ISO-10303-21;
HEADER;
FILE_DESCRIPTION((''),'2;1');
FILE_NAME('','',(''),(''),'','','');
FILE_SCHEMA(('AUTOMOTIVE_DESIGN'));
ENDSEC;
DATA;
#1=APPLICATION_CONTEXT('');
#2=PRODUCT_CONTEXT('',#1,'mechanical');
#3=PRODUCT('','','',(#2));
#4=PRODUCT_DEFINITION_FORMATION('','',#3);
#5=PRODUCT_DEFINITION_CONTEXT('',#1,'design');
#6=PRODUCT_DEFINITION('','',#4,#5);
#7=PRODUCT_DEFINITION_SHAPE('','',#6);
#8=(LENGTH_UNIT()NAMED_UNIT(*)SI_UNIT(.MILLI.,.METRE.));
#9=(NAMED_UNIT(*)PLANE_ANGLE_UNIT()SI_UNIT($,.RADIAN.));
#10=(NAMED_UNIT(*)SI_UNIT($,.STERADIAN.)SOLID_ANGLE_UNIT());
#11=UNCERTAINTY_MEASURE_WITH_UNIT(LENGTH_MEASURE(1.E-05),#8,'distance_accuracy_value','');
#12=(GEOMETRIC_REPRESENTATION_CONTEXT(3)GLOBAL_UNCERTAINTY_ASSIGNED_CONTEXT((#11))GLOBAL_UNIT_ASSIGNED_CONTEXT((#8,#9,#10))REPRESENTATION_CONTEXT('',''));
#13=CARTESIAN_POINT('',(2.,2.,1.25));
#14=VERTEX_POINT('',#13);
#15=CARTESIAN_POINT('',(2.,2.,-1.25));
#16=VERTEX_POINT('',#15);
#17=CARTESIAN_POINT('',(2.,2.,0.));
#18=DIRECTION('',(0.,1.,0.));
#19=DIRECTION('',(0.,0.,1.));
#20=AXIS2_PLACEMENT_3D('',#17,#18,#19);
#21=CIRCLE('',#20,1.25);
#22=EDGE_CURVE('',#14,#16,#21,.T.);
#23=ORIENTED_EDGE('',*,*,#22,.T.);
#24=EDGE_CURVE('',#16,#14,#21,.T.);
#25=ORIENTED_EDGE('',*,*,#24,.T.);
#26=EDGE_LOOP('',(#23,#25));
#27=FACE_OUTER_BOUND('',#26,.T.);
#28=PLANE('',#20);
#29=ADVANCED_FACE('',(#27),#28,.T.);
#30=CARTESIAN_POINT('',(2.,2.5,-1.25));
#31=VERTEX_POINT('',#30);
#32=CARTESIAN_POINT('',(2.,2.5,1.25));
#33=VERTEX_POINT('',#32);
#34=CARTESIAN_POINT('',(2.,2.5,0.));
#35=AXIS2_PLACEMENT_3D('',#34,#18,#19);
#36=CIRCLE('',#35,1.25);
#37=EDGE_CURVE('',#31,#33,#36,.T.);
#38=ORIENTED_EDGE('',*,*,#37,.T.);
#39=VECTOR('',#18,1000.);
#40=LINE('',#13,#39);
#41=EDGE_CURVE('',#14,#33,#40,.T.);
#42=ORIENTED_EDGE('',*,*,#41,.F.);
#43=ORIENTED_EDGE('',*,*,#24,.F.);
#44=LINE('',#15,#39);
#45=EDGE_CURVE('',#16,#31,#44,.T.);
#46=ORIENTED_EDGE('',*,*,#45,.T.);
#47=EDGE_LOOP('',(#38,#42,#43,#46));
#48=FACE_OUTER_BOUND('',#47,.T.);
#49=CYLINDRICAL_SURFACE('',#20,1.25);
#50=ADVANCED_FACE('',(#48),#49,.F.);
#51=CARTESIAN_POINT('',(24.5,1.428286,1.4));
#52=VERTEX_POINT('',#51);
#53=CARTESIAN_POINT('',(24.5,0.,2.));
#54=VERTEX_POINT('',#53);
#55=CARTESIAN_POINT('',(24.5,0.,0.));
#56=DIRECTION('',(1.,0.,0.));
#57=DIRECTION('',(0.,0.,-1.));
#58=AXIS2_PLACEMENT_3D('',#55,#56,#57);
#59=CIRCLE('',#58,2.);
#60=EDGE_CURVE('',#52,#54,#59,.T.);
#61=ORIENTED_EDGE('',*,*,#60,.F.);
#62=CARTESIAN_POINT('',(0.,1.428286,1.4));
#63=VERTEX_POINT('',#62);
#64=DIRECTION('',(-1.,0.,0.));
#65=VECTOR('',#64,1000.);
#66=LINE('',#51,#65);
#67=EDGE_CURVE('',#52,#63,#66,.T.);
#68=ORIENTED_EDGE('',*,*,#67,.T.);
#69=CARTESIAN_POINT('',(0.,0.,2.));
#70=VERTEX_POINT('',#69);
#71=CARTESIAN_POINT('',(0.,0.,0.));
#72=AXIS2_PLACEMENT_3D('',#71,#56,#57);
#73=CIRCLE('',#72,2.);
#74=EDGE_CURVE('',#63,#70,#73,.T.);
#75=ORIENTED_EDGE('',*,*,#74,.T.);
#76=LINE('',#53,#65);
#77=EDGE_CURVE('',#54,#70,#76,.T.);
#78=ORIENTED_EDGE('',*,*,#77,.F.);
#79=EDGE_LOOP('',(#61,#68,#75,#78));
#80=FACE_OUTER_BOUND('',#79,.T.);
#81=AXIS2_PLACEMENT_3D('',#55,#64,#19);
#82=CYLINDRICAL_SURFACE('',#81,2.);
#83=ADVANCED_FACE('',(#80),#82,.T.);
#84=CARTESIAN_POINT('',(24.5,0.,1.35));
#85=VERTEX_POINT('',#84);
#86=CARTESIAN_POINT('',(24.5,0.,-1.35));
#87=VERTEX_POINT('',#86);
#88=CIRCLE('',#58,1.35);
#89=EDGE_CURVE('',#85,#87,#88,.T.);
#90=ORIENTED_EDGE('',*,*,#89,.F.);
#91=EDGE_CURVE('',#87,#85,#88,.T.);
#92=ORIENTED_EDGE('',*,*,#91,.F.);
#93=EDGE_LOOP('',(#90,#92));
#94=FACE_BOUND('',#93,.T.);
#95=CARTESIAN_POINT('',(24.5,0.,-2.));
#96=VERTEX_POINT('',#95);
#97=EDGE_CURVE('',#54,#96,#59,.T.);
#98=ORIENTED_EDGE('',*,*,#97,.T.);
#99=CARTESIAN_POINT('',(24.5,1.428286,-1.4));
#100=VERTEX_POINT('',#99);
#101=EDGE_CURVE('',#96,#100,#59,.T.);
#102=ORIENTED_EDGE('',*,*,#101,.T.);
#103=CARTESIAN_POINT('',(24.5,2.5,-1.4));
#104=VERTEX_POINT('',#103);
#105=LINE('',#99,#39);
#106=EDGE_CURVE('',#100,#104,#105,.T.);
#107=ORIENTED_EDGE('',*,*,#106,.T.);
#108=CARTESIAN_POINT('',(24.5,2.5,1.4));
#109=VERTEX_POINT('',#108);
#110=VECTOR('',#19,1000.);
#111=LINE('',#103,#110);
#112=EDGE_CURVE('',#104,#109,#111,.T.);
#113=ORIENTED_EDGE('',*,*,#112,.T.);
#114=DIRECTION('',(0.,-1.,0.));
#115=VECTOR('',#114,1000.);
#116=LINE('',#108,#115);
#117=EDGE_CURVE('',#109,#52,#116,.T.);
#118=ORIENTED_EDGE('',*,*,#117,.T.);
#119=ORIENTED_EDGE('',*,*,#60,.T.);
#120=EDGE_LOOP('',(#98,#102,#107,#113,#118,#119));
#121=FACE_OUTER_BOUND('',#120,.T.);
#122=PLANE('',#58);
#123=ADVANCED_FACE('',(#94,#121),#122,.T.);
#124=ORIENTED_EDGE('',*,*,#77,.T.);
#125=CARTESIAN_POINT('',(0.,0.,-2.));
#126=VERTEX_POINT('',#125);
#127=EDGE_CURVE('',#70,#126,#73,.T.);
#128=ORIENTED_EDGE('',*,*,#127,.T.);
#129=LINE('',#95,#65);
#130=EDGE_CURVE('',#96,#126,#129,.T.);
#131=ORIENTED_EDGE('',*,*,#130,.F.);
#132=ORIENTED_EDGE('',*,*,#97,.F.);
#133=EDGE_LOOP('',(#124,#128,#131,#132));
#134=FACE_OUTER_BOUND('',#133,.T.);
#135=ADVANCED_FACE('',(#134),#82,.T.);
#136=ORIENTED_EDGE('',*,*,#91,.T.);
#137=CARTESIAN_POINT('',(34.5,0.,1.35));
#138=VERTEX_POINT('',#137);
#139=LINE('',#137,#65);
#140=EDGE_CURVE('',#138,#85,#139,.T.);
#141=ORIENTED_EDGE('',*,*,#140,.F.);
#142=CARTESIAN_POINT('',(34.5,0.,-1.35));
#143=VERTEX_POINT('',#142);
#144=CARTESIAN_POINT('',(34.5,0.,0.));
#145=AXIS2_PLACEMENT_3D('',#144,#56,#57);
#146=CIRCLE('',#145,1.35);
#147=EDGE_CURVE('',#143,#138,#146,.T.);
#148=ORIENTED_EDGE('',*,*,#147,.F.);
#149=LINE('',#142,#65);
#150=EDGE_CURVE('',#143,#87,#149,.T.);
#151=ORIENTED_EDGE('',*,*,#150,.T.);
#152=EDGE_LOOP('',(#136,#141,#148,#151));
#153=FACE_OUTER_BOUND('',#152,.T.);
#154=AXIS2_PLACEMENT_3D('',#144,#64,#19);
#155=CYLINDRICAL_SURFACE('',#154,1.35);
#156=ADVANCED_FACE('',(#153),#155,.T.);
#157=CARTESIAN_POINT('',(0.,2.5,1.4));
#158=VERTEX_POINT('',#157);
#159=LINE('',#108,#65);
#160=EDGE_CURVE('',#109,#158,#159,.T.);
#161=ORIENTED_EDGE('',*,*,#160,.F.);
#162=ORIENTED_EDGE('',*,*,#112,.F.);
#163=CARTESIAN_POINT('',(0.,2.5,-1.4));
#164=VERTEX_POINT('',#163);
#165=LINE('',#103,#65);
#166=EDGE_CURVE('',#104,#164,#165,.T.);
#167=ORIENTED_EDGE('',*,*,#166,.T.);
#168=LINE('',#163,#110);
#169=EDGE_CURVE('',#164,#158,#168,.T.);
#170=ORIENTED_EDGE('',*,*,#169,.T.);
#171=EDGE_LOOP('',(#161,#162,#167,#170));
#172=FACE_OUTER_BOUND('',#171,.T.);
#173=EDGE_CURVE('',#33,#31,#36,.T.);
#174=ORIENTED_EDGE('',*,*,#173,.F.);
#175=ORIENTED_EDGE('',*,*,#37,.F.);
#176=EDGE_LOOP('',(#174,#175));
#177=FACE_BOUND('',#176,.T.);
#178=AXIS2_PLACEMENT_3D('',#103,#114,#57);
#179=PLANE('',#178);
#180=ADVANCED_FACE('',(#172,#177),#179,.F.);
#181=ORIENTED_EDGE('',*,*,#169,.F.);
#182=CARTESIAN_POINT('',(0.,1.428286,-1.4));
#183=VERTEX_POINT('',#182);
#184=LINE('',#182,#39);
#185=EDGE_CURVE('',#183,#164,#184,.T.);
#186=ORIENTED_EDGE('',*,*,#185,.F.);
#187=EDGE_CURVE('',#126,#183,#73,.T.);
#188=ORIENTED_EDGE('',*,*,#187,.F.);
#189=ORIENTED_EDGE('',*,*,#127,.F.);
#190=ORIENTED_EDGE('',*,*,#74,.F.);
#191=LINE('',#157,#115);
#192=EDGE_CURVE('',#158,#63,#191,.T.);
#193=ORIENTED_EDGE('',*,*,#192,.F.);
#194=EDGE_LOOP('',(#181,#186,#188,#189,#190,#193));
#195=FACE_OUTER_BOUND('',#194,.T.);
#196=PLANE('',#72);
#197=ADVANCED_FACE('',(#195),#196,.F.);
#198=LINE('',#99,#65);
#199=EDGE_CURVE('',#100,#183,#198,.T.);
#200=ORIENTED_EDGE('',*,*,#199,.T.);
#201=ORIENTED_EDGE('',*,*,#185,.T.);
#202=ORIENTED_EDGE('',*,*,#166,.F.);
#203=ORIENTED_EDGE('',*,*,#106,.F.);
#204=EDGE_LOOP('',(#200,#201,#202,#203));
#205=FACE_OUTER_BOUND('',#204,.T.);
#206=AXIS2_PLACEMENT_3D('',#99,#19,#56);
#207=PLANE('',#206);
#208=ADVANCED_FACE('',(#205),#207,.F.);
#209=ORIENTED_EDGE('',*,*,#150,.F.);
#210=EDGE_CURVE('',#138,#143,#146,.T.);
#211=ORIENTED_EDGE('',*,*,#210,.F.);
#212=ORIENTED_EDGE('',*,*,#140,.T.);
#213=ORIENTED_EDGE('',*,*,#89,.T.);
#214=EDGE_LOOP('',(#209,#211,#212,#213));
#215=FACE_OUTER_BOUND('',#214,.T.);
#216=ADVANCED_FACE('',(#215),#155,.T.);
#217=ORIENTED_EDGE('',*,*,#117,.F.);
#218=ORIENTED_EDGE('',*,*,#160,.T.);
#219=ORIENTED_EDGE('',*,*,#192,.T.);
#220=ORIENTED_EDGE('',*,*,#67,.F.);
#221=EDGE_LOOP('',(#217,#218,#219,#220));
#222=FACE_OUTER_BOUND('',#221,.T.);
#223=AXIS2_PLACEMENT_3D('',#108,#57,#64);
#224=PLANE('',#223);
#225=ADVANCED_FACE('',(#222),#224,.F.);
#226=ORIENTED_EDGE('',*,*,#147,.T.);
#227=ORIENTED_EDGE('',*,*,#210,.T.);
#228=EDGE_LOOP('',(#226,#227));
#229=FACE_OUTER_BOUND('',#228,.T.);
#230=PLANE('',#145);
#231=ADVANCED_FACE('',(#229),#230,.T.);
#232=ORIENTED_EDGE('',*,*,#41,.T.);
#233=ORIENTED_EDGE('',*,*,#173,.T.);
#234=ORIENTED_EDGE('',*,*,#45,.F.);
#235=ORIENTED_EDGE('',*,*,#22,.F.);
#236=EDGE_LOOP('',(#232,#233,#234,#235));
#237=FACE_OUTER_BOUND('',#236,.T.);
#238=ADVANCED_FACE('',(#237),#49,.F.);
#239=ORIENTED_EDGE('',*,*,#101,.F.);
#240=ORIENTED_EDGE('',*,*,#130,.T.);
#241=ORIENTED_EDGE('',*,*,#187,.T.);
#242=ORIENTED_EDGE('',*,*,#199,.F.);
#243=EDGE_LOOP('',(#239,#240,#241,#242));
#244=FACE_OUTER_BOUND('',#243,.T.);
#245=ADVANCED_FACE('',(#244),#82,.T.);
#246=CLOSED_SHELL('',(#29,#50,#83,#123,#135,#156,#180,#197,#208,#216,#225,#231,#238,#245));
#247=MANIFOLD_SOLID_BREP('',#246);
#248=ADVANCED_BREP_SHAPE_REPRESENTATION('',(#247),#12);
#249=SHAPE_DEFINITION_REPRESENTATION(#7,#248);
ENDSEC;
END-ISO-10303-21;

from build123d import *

# Parameters (mm, degrees)
BOSS_EXTRUDE1_DEPTH = 24.5
SKETCH2_R           = 1.35
BOSS_EXTRUDE2_DEPTH = 10
SKETCH3_R           = 1.25
CUT_EXTRUDE1_DEPTH  = 0.5


with BuildPart() as part:
    # Sketch1 → Boss-Extrude1 (new body)
    with BuildSketch(Plane(origin=(0, 0, 0), x_dir=(0, 0, -1), z_dir=(1, 0, 0))):
        with BuildLine():
            Line((1.4, 1.428285686), (1.4, 2.5))
            Line((1.4, 2.5), (-1.4, 2.5))
            Line((-1.4, 2.5), (-1.4, 1.428285686))
            ThreePointArc((-1.4, 1.428285686), (0, -2), (1.4, 1.428285686))
        make_face()
    extrude(amount=BOSS_EXTRUDE1_DEPTH)

    # Sketch2 → Boss-Extrude2 (add)
    with BuildSketch(Plane(origin=(24.5, 0, 0), x_dir=(0, 0, -1), z_dir=(1, 0, 0))):
        Circle(SKETCH2_R)
    extrude(amount=BOSS_EXTRUDE2_DEPTH)

    # Sketch3 → Cut-Extrude1 (cut)
    with BuildSketch(Plane(origin=(0, 2.5, 0), x_dir=(-1, 0, 0), z_dir=(0, 1, 0))):
        with Locations(Location((-2, 0, 0), (0, 0, 90))):
            Circle(SKETCH3_R)
    extrude(amount=-CUT_EXTRUDE1_DEPTH, mode=Mode.SUBTRACT)


solid = part.part
